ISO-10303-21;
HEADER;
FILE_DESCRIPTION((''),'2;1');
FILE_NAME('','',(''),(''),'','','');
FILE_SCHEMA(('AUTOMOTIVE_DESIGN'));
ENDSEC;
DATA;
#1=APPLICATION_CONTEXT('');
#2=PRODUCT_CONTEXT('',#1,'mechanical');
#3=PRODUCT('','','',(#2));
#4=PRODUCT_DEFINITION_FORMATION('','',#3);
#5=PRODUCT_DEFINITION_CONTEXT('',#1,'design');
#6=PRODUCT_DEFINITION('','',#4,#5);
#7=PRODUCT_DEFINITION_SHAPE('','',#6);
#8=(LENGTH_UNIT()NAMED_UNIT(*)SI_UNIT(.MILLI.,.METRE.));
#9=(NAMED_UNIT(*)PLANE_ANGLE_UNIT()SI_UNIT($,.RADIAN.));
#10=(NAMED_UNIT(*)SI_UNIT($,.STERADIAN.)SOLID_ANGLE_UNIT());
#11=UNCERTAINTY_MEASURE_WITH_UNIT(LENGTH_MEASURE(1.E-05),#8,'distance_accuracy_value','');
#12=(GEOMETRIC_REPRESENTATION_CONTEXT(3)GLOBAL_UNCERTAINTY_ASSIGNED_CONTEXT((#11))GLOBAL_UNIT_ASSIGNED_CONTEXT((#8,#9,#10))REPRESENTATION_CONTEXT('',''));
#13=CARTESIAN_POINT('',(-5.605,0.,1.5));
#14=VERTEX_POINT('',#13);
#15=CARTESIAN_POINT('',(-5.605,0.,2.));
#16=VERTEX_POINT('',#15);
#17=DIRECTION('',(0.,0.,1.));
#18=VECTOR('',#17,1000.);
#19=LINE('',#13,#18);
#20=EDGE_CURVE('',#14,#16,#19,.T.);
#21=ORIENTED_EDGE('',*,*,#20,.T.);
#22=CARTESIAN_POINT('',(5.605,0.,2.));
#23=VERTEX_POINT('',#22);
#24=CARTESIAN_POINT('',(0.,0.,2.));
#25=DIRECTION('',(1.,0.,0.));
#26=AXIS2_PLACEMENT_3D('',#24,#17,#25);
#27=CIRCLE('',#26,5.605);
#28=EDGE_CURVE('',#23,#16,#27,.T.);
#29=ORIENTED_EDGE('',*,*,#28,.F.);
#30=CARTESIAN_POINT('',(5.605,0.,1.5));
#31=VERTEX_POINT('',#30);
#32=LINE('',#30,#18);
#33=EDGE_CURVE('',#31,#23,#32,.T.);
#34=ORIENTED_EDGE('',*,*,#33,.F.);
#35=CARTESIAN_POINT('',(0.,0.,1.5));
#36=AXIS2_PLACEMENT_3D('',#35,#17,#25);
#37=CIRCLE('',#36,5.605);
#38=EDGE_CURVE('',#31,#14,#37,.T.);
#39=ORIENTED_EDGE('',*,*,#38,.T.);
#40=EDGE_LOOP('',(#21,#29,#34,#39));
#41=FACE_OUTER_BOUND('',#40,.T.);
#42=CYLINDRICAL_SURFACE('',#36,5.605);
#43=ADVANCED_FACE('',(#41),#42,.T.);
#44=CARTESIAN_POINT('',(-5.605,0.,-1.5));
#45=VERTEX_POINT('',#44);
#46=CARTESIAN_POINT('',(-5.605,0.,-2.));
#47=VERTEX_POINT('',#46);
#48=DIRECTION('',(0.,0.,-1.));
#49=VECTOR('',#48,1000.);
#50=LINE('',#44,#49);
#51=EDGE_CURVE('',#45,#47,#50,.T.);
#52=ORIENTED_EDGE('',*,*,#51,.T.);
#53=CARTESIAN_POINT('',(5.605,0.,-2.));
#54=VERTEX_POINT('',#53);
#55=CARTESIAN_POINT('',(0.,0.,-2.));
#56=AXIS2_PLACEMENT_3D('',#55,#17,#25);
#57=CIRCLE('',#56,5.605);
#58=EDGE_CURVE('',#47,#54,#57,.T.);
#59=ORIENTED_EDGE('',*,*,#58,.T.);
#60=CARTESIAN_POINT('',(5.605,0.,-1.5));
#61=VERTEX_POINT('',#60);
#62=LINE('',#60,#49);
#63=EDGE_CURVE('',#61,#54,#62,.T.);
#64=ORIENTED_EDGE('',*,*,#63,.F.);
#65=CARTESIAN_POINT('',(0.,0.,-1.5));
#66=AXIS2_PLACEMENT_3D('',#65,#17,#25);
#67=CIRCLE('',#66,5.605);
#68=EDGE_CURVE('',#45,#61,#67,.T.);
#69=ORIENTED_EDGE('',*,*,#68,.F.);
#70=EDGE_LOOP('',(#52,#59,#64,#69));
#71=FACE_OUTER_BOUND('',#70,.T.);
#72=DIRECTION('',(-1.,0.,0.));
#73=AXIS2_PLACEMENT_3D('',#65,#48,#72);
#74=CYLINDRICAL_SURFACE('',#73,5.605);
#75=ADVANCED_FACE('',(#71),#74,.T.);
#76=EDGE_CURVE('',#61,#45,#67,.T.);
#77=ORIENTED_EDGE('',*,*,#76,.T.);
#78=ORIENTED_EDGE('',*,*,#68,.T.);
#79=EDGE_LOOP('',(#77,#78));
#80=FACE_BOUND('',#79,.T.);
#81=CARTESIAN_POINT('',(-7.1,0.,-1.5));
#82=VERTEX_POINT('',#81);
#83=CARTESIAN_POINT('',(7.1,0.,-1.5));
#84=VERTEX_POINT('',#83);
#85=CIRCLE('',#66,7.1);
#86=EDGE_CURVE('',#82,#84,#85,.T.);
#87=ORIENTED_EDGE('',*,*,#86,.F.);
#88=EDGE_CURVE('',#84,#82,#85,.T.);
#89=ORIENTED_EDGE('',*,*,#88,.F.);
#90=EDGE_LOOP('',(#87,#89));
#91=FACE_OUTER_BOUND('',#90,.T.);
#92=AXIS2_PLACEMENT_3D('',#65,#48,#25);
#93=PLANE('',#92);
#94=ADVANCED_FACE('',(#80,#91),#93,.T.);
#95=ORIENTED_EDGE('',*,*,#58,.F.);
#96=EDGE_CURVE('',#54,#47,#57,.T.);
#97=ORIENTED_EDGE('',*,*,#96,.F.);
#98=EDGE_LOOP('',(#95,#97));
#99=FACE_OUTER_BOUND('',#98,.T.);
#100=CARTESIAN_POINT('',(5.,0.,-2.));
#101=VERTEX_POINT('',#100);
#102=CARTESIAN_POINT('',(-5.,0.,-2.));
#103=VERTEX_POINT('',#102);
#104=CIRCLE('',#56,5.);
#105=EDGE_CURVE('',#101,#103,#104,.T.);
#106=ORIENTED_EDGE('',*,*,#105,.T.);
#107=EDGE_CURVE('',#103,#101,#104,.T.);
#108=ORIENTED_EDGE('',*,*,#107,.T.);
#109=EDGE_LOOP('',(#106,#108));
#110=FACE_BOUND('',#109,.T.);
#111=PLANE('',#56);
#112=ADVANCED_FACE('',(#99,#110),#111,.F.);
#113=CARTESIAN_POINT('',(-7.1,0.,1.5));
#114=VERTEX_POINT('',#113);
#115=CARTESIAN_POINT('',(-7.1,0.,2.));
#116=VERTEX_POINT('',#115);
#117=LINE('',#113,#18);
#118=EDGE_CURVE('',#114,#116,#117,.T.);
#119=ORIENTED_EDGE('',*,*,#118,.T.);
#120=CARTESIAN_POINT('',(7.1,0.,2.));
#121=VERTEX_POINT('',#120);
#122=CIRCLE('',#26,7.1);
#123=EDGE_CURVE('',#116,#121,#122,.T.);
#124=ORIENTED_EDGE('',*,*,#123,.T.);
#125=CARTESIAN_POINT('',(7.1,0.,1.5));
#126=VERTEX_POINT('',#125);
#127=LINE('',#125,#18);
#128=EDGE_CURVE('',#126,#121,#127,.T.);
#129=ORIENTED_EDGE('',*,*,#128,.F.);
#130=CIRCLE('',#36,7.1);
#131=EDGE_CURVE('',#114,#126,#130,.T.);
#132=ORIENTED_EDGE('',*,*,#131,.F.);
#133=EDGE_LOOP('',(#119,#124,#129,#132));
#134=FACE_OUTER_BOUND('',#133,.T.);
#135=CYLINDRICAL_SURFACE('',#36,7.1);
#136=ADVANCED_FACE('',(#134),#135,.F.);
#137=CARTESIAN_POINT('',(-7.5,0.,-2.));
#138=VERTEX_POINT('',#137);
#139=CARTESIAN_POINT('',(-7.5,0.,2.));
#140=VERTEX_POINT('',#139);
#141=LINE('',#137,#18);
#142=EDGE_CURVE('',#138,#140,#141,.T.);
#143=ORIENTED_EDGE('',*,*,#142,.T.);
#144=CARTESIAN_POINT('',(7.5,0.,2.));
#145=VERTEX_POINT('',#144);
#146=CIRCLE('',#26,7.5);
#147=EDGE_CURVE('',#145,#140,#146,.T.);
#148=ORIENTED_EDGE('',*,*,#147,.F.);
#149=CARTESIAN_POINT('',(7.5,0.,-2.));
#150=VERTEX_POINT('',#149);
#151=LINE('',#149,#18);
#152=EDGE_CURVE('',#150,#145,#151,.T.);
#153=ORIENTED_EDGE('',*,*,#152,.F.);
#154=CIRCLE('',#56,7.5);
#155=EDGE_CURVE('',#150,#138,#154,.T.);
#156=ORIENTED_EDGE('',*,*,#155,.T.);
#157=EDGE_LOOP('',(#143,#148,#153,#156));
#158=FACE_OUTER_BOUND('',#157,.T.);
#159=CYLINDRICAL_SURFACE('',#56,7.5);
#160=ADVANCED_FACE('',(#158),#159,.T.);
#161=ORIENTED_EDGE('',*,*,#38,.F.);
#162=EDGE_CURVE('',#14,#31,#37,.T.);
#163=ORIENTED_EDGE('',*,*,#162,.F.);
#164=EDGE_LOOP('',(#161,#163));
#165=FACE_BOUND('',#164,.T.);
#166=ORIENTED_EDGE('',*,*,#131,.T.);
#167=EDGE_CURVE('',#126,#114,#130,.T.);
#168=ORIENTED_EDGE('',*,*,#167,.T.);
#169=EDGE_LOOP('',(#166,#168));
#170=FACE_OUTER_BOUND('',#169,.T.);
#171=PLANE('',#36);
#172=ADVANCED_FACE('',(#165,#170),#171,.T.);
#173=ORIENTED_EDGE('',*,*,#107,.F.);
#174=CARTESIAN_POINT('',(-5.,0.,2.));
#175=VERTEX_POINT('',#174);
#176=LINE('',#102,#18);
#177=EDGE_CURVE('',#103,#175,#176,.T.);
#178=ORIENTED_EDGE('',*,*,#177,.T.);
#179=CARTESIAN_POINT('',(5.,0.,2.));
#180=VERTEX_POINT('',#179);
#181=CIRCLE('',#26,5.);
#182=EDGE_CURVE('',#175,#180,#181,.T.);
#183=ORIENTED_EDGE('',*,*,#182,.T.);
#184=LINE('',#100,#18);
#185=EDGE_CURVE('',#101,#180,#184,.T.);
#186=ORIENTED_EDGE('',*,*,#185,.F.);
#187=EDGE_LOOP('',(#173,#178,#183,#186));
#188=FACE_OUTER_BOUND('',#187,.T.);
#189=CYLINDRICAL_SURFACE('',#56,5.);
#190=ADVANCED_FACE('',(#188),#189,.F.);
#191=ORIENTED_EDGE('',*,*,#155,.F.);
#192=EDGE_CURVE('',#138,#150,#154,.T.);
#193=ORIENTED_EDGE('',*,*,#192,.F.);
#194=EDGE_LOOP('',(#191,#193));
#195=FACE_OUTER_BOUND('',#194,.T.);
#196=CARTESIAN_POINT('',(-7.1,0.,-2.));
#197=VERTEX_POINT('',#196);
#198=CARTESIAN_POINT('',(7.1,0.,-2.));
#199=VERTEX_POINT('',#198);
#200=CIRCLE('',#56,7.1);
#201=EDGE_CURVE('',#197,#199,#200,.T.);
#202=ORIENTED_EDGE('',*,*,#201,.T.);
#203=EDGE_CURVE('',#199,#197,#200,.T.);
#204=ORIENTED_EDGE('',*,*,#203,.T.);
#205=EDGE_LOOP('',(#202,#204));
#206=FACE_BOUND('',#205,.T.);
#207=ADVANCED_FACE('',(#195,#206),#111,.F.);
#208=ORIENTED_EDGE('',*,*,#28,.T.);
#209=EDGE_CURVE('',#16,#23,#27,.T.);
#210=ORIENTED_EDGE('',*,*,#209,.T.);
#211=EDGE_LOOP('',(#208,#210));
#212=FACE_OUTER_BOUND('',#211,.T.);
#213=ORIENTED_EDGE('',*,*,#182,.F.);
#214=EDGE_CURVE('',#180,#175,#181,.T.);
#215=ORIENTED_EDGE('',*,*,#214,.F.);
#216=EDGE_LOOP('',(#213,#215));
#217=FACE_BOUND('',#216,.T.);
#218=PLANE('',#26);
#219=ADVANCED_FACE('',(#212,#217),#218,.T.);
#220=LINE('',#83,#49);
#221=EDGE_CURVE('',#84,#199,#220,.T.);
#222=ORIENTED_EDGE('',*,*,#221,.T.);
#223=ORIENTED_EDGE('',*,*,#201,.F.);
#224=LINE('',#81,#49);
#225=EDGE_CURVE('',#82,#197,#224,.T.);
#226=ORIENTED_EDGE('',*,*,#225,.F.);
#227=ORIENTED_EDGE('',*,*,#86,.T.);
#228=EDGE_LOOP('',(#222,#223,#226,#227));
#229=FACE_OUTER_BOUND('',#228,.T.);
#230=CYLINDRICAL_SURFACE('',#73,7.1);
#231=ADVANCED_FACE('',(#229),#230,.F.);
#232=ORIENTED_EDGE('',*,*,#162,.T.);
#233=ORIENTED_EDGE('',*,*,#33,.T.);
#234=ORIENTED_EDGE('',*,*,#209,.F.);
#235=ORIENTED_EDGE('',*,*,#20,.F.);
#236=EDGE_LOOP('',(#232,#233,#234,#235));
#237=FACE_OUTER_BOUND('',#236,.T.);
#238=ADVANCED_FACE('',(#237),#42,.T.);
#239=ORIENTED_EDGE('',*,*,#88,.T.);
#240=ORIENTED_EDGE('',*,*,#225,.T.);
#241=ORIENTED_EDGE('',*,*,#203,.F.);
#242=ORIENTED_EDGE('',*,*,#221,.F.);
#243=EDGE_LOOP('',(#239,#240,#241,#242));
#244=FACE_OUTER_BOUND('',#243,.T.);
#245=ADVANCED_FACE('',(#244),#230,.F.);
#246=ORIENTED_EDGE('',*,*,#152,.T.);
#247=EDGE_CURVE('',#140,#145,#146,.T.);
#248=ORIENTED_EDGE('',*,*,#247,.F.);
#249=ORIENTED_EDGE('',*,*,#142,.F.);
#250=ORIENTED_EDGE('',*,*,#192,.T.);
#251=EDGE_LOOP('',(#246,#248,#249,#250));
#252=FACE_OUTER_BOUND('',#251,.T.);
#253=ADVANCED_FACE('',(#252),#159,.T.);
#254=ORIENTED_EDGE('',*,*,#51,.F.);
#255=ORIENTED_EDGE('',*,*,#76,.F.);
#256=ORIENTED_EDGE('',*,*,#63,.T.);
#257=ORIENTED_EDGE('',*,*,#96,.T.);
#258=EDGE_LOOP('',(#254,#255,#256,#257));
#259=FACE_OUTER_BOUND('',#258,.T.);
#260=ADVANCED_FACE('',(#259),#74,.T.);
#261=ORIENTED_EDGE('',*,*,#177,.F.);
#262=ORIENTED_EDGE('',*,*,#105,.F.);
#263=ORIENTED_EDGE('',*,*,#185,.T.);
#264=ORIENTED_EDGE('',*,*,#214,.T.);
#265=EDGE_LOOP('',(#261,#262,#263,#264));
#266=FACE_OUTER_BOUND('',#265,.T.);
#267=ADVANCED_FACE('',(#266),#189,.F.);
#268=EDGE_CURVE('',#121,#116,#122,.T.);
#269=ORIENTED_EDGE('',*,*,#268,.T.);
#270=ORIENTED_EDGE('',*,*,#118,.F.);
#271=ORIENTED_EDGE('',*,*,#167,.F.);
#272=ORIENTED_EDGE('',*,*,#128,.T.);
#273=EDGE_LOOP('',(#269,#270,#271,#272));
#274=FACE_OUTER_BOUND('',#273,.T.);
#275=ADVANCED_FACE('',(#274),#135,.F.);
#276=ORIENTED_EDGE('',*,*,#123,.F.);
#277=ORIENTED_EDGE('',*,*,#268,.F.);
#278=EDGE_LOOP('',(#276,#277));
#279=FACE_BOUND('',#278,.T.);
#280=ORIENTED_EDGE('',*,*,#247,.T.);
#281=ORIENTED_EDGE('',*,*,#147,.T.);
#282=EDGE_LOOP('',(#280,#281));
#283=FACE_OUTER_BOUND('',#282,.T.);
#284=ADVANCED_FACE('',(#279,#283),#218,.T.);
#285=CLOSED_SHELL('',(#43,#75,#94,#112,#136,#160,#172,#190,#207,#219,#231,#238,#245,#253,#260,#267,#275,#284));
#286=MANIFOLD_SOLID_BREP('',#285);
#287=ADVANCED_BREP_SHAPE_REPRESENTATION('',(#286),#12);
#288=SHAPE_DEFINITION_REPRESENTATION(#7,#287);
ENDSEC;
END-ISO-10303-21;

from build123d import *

# Parameters (mm, degrees)
BOSS_EXTRUDE1_DEPTH      = 2
BOSS_EXTRUDE1_DEPTH_BACK = 2
SKETCH1_R                = 7.5
SKETCH1_R_2              = 5
SKETCH2_R                = 7.1
SKETCH2_R_2              = 5.605
CUT_EXTRUDE1_DEPTH       = 0.5


with BuildPart() as part:
    # Sketch1 → Boss-Extrude1 (new, two sides: drawn at the far end of the back side and taken through both)
    with BuildSketch(Plane.XY.offset(-BOSS_EXTRUDE1_DEPTH_BACK)):
        Circle(SKETCH1_R)
        Circle(SKETCH1_R_2, mode=Mode.SUBTRACT)
    extrude(amount=BOSS_EXTRUDE1_DEPTH + BOSS_EXTRUDE1_DEPTH_BACK)

    # Sketch2 → Cut-Extrude1 (cut)
    with BuildSketch(Plane.XY.offset(2)):
        Circle(SKETCH2_R)
        Circle(SKETCH2_R_2, mode=Mode.SUBTRACT)
    cut_extrude1 = extrude(amount=-CUT_EXTRUDE1_DEPTH, mode=Mode.SUBTRACT)

    # Mirror1: Cut-Extrude1 across plane
    add(cut_extrude1.mirror(Plane.XY), mode=Mode.SUBTRACT)


solid = part.part
